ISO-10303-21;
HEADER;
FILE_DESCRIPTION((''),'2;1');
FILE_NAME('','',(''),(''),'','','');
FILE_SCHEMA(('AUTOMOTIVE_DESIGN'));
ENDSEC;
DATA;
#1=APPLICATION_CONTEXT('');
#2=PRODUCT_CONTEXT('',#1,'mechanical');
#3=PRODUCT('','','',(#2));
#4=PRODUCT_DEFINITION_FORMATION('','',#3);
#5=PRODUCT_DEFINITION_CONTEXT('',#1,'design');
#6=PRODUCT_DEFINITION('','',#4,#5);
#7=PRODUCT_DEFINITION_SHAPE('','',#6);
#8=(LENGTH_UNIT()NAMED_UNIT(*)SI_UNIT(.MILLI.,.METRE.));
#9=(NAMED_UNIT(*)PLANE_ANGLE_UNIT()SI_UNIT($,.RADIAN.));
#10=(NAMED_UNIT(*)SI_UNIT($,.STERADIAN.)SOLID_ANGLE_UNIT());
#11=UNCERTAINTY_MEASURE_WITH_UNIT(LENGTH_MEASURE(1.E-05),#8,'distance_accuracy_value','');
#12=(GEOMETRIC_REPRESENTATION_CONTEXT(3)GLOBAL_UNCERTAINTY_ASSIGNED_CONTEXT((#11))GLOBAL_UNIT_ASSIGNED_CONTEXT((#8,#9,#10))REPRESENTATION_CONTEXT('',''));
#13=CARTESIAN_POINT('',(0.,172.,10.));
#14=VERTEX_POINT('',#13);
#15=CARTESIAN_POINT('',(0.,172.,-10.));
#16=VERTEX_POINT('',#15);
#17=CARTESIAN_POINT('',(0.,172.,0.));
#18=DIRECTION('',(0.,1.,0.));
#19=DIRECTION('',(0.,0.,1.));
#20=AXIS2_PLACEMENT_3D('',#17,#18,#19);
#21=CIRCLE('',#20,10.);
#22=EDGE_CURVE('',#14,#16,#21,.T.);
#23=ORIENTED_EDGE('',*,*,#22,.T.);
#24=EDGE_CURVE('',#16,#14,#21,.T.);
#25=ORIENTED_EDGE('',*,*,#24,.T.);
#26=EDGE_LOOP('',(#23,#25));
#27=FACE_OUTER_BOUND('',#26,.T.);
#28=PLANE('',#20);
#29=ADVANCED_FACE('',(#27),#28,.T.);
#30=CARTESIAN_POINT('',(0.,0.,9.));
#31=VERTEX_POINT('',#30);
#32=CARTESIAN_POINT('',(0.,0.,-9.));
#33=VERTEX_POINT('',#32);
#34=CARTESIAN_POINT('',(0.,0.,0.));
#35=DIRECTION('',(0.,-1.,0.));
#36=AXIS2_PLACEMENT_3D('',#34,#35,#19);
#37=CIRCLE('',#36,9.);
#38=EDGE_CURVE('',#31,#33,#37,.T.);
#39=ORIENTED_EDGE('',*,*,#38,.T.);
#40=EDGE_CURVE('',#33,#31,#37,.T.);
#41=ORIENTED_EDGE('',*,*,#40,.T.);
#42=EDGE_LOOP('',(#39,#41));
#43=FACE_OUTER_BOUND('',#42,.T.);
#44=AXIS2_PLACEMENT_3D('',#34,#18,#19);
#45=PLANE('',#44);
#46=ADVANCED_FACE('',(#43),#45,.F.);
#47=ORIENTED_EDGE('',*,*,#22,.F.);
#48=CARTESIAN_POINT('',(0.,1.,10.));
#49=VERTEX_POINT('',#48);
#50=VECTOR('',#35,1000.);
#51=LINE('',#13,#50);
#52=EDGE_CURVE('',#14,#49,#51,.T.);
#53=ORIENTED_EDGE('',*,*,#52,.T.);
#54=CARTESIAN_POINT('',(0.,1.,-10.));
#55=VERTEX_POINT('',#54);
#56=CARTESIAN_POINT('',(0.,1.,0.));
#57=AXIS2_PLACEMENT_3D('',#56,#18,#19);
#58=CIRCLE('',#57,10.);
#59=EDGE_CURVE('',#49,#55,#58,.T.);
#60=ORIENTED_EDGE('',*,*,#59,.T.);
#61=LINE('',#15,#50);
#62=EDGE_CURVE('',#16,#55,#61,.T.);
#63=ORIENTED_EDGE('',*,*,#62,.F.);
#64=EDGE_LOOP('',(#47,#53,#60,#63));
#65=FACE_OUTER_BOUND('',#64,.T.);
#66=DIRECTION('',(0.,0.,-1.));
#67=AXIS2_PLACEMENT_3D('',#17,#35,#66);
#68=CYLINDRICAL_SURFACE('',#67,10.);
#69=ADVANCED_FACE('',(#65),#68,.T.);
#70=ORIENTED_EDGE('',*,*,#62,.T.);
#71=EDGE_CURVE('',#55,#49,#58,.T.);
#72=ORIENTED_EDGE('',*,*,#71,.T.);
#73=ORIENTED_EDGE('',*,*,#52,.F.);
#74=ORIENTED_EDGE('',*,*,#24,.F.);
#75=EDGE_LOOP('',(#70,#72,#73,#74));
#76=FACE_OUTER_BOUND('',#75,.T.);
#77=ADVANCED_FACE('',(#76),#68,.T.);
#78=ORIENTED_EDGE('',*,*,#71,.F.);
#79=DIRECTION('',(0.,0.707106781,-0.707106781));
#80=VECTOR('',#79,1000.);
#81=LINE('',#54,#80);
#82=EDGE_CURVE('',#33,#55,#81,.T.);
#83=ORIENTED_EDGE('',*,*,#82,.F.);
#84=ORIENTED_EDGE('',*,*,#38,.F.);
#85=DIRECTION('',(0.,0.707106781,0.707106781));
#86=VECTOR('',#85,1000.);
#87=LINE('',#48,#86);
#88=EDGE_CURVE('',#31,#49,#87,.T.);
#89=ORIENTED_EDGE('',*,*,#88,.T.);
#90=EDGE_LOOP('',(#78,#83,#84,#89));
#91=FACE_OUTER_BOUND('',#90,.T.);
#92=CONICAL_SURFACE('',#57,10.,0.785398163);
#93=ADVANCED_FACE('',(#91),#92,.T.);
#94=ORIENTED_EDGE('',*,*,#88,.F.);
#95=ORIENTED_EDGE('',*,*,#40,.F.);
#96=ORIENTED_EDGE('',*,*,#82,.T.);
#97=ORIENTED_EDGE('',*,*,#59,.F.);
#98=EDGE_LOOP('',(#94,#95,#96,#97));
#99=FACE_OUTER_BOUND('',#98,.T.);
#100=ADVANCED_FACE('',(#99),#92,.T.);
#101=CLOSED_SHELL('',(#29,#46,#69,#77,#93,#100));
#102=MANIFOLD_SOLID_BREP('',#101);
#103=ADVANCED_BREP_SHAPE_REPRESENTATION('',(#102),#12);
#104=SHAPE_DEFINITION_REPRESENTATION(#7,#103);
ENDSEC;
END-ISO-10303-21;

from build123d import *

# Parameters (mm, degrees)
SKETCH2_R           = 10
BOSS_EXTRUDE1_DEPTH = 172
CHAMFER1_SIZE       = 1


with BuildPart() as part:
    # Sketch2 → Boss-Extrude1 (new body)
    with BuildSketch(Plane(origin=(0, 0, 0), x_dir=(1, 0, 0), z_dir=(0, 1, 0))):
        with Locations(Location((0, 0, 0), (0, 0, 270))):
            Circle(SKETCH2_R)
    extrude(amount=BOSS_EXTRUDE1_DEPTH)

    # Chamfer1
    chamfer1_edges = [part.edges().sort_by_distance(p)[0] for p in [
        (0, 0, -10),
    ]]
    chamfer(chamfer1_edges, length=CHAMFER1_SIZE)


solid = part.part
